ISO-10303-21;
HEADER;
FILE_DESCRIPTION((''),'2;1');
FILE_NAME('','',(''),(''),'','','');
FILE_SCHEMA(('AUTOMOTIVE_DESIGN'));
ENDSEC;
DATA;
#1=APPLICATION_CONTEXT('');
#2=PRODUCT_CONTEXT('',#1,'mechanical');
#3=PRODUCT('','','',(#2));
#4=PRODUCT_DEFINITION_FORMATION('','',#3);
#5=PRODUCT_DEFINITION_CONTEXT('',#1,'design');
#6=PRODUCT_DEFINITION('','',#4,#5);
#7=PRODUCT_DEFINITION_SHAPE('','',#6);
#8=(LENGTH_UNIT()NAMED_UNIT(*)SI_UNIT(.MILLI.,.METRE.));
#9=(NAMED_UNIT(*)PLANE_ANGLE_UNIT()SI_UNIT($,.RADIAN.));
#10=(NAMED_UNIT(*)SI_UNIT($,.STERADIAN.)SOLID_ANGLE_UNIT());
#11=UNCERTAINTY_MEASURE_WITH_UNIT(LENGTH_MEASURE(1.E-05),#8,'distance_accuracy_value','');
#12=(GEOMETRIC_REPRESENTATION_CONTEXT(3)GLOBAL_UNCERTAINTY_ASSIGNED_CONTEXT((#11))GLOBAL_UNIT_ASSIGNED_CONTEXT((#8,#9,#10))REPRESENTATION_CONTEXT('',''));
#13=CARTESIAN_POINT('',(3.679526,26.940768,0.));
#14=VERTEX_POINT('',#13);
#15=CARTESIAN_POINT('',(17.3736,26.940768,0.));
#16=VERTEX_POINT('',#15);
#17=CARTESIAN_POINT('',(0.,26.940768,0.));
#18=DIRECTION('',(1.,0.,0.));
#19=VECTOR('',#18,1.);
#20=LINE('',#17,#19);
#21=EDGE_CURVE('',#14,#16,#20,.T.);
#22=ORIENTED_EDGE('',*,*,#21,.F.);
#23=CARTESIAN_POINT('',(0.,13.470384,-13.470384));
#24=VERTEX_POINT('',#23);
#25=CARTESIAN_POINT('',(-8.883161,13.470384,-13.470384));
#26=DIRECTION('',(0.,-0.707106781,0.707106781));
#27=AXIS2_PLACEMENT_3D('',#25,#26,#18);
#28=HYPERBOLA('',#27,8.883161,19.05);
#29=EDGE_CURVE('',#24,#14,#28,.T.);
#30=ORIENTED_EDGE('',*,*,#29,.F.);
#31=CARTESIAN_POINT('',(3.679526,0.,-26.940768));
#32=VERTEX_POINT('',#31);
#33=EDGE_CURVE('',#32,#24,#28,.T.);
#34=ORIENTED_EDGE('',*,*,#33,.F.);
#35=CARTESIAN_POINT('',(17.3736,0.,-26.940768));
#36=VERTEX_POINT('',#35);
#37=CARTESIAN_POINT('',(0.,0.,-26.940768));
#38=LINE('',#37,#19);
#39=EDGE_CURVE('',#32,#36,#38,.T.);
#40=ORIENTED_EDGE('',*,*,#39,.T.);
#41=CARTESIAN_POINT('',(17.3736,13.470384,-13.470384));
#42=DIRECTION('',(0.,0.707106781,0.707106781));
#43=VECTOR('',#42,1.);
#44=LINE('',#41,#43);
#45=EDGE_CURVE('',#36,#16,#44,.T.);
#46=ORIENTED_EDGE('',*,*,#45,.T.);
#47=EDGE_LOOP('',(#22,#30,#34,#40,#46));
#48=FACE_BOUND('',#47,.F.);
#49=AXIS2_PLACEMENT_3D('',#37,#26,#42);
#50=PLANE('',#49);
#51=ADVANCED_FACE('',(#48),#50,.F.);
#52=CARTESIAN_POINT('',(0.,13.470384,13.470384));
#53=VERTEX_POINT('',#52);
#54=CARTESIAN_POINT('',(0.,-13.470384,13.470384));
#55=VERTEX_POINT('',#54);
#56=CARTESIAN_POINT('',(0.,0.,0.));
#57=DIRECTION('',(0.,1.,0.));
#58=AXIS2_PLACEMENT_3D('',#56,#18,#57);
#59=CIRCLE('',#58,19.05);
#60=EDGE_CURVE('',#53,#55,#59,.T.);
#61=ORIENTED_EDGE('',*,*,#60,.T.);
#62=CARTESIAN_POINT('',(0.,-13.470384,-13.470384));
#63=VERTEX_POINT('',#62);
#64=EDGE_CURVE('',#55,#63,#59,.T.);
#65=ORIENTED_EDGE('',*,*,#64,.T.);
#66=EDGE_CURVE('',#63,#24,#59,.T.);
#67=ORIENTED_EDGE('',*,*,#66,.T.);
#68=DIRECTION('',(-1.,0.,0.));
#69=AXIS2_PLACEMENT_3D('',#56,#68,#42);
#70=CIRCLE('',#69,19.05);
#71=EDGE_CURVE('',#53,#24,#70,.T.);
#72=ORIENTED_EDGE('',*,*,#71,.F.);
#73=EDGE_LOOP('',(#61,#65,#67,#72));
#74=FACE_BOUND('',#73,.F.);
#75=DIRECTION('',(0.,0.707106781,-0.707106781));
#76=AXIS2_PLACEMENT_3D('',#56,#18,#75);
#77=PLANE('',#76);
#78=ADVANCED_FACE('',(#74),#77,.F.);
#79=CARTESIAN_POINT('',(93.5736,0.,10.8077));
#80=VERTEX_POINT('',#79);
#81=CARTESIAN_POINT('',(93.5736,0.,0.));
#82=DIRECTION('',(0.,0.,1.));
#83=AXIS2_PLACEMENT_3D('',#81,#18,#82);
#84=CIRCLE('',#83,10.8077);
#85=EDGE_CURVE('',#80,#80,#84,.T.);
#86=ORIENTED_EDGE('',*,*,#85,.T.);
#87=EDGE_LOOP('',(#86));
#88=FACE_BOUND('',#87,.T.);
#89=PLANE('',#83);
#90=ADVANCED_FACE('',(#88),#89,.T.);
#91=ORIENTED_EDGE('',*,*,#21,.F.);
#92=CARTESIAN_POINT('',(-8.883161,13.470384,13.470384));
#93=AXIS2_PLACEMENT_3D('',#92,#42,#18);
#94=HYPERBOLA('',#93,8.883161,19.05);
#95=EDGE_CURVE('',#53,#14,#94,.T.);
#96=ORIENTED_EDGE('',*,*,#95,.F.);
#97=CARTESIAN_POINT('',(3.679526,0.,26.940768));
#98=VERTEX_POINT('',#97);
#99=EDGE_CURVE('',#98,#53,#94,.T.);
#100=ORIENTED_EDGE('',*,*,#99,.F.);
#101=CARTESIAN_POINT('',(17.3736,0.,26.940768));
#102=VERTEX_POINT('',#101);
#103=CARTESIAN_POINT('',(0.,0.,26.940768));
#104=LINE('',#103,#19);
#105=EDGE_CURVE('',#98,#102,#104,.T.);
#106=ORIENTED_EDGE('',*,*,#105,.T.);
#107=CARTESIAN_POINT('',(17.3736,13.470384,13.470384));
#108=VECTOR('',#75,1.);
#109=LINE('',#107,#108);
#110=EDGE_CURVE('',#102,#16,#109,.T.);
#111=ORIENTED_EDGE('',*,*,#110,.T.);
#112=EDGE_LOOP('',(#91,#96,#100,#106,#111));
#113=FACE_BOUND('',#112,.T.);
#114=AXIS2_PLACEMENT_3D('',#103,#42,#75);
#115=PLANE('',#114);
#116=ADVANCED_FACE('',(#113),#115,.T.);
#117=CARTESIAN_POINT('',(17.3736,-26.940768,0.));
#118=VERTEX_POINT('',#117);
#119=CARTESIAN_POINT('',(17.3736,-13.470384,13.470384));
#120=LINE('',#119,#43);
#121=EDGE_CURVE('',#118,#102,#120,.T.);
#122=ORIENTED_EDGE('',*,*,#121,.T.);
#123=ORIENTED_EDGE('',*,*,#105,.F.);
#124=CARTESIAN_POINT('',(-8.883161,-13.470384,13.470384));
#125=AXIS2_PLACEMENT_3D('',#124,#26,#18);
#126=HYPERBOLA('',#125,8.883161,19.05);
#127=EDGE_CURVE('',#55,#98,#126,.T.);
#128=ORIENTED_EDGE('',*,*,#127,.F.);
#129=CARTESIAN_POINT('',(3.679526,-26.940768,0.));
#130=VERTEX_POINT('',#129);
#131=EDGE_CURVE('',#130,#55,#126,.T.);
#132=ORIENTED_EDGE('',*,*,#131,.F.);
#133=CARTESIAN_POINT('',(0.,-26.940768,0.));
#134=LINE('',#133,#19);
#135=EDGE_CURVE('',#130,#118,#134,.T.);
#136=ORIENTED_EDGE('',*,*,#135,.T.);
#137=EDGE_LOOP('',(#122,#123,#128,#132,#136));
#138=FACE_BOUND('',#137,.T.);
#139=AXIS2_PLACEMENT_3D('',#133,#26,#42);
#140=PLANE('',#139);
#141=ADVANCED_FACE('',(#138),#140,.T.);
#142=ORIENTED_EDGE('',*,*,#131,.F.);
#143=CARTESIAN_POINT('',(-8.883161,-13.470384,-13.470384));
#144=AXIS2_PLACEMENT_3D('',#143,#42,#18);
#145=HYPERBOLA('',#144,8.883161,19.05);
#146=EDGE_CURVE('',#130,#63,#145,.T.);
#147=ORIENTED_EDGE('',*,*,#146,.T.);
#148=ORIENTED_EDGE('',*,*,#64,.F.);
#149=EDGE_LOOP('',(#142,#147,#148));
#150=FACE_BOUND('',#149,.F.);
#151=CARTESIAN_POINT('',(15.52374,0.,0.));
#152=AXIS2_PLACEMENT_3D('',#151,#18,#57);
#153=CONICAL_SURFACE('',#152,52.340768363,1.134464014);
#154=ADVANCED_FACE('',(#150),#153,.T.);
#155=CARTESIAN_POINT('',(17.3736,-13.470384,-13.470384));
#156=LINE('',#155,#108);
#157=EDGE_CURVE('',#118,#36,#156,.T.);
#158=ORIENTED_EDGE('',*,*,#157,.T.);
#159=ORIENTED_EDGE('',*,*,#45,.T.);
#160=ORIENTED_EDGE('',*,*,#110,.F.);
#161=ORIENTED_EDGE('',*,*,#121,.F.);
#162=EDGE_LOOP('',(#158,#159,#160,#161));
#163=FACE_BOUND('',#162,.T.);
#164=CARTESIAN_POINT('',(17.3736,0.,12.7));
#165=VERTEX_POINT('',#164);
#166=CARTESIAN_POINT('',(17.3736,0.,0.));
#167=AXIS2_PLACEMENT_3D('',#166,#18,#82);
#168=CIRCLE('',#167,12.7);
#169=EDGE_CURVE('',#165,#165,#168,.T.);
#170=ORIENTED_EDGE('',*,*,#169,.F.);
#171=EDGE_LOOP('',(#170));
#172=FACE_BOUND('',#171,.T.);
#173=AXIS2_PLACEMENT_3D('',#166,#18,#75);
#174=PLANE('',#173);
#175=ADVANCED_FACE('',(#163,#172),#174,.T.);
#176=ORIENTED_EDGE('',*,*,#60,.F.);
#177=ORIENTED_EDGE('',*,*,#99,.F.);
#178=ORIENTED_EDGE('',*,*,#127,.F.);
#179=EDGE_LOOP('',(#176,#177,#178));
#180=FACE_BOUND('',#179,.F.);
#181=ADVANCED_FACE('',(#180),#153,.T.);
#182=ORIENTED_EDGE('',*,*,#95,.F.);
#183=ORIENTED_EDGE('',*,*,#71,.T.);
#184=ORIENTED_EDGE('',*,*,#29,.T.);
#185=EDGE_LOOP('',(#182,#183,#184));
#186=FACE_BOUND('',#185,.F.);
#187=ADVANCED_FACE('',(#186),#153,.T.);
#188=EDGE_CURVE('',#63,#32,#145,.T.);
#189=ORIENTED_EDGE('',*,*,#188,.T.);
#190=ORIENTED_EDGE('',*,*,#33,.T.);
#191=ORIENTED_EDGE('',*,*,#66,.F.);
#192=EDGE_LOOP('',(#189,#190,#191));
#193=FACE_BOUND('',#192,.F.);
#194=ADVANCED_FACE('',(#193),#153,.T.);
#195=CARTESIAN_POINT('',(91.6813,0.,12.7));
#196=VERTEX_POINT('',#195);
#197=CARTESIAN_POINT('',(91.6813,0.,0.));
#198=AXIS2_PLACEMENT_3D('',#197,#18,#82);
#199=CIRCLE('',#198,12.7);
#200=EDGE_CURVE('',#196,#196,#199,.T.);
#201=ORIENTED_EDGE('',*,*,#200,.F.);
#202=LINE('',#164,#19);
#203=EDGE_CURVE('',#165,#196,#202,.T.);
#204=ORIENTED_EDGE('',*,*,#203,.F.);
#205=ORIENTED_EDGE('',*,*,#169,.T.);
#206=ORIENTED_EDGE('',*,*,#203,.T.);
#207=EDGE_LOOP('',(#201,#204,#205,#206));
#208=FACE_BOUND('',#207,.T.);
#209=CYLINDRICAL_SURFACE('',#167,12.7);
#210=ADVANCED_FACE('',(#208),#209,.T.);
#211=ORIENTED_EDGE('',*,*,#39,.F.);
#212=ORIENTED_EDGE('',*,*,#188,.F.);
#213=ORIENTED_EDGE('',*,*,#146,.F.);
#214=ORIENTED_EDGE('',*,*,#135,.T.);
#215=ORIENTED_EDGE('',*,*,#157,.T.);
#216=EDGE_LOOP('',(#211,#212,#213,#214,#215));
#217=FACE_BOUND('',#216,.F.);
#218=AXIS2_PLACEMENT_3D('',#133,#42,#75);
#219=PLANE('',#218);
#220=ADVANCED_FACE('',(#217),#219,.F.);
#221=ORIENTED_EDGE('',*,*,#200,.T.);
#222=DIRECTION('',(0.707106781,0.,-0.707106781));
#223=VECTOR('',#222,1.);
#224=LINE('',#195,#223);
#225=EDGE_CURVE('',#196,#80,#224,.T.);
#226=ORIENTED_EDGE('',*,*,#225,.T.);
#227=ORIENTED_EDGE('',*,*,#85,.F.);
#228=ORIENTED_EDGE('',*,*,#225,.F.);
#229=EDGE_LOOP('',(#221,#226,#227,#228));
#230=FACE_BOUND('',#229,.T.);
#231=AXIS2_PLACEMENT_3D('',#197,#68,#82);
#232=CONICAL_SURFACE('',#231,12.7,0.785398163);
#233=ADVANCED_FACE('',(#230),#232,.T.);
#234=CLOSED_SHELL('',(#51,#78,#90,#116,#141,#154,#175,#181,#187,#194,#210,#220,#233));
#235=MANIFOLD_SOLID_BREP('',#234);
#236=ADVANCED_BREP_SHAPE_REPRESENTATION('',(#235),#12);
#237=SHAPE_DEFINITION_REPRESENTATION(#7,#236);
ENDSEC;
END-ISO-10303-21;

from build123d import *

# Parameters (mm, degrees)
SKETCH1_W      = 38.1
SKETCH1_H      = 38.1
BASEHEAD_DEPTH = 17.3736


with BuildPart() as part:
    # Sketch1 → BaseHead (new body)
    with BuildSketch(Plane(origin=(0, 0, 0), x_dir=(0, 0.7071067811865488, -0.7071067811865462), z_dir=(1, 0, 0))):
        Rectangle(SKETCH1_W, SKETCH1_H)
    extrude(amount=BASEHEAD_DEPTH)

    # BodySke → Body (revolve)
    with BuildSketch(Plane.XY, mode=Mode.PRIVATE) as body_sk:
        Polygon((17.3736, 0), (17.3736, 12.7), (91.6813, 12.7), (93.5736, 10.8077), (93.5736, 0), align=None)
    revolve(body_sk.sketch.rotate(Axis((0, 0, 0), (1, 0, 0)), 90), axis=Axis((0, 0, 0), (1, 0, 0)))

    # Sketch3 → HeadChamfer (revolve, cut)
    with BuildSketch(Plane.XY):
        Polygon((0, 19.05), (-12.7, 19.05), (-12.7, 52.340768363), (15.523740234, 52.340768363), align=None)
    revolve(axis=Axis((0, 0, 0), (1, 0, 0)), mode=Mode.SUBTRACT)


solid = part.part
